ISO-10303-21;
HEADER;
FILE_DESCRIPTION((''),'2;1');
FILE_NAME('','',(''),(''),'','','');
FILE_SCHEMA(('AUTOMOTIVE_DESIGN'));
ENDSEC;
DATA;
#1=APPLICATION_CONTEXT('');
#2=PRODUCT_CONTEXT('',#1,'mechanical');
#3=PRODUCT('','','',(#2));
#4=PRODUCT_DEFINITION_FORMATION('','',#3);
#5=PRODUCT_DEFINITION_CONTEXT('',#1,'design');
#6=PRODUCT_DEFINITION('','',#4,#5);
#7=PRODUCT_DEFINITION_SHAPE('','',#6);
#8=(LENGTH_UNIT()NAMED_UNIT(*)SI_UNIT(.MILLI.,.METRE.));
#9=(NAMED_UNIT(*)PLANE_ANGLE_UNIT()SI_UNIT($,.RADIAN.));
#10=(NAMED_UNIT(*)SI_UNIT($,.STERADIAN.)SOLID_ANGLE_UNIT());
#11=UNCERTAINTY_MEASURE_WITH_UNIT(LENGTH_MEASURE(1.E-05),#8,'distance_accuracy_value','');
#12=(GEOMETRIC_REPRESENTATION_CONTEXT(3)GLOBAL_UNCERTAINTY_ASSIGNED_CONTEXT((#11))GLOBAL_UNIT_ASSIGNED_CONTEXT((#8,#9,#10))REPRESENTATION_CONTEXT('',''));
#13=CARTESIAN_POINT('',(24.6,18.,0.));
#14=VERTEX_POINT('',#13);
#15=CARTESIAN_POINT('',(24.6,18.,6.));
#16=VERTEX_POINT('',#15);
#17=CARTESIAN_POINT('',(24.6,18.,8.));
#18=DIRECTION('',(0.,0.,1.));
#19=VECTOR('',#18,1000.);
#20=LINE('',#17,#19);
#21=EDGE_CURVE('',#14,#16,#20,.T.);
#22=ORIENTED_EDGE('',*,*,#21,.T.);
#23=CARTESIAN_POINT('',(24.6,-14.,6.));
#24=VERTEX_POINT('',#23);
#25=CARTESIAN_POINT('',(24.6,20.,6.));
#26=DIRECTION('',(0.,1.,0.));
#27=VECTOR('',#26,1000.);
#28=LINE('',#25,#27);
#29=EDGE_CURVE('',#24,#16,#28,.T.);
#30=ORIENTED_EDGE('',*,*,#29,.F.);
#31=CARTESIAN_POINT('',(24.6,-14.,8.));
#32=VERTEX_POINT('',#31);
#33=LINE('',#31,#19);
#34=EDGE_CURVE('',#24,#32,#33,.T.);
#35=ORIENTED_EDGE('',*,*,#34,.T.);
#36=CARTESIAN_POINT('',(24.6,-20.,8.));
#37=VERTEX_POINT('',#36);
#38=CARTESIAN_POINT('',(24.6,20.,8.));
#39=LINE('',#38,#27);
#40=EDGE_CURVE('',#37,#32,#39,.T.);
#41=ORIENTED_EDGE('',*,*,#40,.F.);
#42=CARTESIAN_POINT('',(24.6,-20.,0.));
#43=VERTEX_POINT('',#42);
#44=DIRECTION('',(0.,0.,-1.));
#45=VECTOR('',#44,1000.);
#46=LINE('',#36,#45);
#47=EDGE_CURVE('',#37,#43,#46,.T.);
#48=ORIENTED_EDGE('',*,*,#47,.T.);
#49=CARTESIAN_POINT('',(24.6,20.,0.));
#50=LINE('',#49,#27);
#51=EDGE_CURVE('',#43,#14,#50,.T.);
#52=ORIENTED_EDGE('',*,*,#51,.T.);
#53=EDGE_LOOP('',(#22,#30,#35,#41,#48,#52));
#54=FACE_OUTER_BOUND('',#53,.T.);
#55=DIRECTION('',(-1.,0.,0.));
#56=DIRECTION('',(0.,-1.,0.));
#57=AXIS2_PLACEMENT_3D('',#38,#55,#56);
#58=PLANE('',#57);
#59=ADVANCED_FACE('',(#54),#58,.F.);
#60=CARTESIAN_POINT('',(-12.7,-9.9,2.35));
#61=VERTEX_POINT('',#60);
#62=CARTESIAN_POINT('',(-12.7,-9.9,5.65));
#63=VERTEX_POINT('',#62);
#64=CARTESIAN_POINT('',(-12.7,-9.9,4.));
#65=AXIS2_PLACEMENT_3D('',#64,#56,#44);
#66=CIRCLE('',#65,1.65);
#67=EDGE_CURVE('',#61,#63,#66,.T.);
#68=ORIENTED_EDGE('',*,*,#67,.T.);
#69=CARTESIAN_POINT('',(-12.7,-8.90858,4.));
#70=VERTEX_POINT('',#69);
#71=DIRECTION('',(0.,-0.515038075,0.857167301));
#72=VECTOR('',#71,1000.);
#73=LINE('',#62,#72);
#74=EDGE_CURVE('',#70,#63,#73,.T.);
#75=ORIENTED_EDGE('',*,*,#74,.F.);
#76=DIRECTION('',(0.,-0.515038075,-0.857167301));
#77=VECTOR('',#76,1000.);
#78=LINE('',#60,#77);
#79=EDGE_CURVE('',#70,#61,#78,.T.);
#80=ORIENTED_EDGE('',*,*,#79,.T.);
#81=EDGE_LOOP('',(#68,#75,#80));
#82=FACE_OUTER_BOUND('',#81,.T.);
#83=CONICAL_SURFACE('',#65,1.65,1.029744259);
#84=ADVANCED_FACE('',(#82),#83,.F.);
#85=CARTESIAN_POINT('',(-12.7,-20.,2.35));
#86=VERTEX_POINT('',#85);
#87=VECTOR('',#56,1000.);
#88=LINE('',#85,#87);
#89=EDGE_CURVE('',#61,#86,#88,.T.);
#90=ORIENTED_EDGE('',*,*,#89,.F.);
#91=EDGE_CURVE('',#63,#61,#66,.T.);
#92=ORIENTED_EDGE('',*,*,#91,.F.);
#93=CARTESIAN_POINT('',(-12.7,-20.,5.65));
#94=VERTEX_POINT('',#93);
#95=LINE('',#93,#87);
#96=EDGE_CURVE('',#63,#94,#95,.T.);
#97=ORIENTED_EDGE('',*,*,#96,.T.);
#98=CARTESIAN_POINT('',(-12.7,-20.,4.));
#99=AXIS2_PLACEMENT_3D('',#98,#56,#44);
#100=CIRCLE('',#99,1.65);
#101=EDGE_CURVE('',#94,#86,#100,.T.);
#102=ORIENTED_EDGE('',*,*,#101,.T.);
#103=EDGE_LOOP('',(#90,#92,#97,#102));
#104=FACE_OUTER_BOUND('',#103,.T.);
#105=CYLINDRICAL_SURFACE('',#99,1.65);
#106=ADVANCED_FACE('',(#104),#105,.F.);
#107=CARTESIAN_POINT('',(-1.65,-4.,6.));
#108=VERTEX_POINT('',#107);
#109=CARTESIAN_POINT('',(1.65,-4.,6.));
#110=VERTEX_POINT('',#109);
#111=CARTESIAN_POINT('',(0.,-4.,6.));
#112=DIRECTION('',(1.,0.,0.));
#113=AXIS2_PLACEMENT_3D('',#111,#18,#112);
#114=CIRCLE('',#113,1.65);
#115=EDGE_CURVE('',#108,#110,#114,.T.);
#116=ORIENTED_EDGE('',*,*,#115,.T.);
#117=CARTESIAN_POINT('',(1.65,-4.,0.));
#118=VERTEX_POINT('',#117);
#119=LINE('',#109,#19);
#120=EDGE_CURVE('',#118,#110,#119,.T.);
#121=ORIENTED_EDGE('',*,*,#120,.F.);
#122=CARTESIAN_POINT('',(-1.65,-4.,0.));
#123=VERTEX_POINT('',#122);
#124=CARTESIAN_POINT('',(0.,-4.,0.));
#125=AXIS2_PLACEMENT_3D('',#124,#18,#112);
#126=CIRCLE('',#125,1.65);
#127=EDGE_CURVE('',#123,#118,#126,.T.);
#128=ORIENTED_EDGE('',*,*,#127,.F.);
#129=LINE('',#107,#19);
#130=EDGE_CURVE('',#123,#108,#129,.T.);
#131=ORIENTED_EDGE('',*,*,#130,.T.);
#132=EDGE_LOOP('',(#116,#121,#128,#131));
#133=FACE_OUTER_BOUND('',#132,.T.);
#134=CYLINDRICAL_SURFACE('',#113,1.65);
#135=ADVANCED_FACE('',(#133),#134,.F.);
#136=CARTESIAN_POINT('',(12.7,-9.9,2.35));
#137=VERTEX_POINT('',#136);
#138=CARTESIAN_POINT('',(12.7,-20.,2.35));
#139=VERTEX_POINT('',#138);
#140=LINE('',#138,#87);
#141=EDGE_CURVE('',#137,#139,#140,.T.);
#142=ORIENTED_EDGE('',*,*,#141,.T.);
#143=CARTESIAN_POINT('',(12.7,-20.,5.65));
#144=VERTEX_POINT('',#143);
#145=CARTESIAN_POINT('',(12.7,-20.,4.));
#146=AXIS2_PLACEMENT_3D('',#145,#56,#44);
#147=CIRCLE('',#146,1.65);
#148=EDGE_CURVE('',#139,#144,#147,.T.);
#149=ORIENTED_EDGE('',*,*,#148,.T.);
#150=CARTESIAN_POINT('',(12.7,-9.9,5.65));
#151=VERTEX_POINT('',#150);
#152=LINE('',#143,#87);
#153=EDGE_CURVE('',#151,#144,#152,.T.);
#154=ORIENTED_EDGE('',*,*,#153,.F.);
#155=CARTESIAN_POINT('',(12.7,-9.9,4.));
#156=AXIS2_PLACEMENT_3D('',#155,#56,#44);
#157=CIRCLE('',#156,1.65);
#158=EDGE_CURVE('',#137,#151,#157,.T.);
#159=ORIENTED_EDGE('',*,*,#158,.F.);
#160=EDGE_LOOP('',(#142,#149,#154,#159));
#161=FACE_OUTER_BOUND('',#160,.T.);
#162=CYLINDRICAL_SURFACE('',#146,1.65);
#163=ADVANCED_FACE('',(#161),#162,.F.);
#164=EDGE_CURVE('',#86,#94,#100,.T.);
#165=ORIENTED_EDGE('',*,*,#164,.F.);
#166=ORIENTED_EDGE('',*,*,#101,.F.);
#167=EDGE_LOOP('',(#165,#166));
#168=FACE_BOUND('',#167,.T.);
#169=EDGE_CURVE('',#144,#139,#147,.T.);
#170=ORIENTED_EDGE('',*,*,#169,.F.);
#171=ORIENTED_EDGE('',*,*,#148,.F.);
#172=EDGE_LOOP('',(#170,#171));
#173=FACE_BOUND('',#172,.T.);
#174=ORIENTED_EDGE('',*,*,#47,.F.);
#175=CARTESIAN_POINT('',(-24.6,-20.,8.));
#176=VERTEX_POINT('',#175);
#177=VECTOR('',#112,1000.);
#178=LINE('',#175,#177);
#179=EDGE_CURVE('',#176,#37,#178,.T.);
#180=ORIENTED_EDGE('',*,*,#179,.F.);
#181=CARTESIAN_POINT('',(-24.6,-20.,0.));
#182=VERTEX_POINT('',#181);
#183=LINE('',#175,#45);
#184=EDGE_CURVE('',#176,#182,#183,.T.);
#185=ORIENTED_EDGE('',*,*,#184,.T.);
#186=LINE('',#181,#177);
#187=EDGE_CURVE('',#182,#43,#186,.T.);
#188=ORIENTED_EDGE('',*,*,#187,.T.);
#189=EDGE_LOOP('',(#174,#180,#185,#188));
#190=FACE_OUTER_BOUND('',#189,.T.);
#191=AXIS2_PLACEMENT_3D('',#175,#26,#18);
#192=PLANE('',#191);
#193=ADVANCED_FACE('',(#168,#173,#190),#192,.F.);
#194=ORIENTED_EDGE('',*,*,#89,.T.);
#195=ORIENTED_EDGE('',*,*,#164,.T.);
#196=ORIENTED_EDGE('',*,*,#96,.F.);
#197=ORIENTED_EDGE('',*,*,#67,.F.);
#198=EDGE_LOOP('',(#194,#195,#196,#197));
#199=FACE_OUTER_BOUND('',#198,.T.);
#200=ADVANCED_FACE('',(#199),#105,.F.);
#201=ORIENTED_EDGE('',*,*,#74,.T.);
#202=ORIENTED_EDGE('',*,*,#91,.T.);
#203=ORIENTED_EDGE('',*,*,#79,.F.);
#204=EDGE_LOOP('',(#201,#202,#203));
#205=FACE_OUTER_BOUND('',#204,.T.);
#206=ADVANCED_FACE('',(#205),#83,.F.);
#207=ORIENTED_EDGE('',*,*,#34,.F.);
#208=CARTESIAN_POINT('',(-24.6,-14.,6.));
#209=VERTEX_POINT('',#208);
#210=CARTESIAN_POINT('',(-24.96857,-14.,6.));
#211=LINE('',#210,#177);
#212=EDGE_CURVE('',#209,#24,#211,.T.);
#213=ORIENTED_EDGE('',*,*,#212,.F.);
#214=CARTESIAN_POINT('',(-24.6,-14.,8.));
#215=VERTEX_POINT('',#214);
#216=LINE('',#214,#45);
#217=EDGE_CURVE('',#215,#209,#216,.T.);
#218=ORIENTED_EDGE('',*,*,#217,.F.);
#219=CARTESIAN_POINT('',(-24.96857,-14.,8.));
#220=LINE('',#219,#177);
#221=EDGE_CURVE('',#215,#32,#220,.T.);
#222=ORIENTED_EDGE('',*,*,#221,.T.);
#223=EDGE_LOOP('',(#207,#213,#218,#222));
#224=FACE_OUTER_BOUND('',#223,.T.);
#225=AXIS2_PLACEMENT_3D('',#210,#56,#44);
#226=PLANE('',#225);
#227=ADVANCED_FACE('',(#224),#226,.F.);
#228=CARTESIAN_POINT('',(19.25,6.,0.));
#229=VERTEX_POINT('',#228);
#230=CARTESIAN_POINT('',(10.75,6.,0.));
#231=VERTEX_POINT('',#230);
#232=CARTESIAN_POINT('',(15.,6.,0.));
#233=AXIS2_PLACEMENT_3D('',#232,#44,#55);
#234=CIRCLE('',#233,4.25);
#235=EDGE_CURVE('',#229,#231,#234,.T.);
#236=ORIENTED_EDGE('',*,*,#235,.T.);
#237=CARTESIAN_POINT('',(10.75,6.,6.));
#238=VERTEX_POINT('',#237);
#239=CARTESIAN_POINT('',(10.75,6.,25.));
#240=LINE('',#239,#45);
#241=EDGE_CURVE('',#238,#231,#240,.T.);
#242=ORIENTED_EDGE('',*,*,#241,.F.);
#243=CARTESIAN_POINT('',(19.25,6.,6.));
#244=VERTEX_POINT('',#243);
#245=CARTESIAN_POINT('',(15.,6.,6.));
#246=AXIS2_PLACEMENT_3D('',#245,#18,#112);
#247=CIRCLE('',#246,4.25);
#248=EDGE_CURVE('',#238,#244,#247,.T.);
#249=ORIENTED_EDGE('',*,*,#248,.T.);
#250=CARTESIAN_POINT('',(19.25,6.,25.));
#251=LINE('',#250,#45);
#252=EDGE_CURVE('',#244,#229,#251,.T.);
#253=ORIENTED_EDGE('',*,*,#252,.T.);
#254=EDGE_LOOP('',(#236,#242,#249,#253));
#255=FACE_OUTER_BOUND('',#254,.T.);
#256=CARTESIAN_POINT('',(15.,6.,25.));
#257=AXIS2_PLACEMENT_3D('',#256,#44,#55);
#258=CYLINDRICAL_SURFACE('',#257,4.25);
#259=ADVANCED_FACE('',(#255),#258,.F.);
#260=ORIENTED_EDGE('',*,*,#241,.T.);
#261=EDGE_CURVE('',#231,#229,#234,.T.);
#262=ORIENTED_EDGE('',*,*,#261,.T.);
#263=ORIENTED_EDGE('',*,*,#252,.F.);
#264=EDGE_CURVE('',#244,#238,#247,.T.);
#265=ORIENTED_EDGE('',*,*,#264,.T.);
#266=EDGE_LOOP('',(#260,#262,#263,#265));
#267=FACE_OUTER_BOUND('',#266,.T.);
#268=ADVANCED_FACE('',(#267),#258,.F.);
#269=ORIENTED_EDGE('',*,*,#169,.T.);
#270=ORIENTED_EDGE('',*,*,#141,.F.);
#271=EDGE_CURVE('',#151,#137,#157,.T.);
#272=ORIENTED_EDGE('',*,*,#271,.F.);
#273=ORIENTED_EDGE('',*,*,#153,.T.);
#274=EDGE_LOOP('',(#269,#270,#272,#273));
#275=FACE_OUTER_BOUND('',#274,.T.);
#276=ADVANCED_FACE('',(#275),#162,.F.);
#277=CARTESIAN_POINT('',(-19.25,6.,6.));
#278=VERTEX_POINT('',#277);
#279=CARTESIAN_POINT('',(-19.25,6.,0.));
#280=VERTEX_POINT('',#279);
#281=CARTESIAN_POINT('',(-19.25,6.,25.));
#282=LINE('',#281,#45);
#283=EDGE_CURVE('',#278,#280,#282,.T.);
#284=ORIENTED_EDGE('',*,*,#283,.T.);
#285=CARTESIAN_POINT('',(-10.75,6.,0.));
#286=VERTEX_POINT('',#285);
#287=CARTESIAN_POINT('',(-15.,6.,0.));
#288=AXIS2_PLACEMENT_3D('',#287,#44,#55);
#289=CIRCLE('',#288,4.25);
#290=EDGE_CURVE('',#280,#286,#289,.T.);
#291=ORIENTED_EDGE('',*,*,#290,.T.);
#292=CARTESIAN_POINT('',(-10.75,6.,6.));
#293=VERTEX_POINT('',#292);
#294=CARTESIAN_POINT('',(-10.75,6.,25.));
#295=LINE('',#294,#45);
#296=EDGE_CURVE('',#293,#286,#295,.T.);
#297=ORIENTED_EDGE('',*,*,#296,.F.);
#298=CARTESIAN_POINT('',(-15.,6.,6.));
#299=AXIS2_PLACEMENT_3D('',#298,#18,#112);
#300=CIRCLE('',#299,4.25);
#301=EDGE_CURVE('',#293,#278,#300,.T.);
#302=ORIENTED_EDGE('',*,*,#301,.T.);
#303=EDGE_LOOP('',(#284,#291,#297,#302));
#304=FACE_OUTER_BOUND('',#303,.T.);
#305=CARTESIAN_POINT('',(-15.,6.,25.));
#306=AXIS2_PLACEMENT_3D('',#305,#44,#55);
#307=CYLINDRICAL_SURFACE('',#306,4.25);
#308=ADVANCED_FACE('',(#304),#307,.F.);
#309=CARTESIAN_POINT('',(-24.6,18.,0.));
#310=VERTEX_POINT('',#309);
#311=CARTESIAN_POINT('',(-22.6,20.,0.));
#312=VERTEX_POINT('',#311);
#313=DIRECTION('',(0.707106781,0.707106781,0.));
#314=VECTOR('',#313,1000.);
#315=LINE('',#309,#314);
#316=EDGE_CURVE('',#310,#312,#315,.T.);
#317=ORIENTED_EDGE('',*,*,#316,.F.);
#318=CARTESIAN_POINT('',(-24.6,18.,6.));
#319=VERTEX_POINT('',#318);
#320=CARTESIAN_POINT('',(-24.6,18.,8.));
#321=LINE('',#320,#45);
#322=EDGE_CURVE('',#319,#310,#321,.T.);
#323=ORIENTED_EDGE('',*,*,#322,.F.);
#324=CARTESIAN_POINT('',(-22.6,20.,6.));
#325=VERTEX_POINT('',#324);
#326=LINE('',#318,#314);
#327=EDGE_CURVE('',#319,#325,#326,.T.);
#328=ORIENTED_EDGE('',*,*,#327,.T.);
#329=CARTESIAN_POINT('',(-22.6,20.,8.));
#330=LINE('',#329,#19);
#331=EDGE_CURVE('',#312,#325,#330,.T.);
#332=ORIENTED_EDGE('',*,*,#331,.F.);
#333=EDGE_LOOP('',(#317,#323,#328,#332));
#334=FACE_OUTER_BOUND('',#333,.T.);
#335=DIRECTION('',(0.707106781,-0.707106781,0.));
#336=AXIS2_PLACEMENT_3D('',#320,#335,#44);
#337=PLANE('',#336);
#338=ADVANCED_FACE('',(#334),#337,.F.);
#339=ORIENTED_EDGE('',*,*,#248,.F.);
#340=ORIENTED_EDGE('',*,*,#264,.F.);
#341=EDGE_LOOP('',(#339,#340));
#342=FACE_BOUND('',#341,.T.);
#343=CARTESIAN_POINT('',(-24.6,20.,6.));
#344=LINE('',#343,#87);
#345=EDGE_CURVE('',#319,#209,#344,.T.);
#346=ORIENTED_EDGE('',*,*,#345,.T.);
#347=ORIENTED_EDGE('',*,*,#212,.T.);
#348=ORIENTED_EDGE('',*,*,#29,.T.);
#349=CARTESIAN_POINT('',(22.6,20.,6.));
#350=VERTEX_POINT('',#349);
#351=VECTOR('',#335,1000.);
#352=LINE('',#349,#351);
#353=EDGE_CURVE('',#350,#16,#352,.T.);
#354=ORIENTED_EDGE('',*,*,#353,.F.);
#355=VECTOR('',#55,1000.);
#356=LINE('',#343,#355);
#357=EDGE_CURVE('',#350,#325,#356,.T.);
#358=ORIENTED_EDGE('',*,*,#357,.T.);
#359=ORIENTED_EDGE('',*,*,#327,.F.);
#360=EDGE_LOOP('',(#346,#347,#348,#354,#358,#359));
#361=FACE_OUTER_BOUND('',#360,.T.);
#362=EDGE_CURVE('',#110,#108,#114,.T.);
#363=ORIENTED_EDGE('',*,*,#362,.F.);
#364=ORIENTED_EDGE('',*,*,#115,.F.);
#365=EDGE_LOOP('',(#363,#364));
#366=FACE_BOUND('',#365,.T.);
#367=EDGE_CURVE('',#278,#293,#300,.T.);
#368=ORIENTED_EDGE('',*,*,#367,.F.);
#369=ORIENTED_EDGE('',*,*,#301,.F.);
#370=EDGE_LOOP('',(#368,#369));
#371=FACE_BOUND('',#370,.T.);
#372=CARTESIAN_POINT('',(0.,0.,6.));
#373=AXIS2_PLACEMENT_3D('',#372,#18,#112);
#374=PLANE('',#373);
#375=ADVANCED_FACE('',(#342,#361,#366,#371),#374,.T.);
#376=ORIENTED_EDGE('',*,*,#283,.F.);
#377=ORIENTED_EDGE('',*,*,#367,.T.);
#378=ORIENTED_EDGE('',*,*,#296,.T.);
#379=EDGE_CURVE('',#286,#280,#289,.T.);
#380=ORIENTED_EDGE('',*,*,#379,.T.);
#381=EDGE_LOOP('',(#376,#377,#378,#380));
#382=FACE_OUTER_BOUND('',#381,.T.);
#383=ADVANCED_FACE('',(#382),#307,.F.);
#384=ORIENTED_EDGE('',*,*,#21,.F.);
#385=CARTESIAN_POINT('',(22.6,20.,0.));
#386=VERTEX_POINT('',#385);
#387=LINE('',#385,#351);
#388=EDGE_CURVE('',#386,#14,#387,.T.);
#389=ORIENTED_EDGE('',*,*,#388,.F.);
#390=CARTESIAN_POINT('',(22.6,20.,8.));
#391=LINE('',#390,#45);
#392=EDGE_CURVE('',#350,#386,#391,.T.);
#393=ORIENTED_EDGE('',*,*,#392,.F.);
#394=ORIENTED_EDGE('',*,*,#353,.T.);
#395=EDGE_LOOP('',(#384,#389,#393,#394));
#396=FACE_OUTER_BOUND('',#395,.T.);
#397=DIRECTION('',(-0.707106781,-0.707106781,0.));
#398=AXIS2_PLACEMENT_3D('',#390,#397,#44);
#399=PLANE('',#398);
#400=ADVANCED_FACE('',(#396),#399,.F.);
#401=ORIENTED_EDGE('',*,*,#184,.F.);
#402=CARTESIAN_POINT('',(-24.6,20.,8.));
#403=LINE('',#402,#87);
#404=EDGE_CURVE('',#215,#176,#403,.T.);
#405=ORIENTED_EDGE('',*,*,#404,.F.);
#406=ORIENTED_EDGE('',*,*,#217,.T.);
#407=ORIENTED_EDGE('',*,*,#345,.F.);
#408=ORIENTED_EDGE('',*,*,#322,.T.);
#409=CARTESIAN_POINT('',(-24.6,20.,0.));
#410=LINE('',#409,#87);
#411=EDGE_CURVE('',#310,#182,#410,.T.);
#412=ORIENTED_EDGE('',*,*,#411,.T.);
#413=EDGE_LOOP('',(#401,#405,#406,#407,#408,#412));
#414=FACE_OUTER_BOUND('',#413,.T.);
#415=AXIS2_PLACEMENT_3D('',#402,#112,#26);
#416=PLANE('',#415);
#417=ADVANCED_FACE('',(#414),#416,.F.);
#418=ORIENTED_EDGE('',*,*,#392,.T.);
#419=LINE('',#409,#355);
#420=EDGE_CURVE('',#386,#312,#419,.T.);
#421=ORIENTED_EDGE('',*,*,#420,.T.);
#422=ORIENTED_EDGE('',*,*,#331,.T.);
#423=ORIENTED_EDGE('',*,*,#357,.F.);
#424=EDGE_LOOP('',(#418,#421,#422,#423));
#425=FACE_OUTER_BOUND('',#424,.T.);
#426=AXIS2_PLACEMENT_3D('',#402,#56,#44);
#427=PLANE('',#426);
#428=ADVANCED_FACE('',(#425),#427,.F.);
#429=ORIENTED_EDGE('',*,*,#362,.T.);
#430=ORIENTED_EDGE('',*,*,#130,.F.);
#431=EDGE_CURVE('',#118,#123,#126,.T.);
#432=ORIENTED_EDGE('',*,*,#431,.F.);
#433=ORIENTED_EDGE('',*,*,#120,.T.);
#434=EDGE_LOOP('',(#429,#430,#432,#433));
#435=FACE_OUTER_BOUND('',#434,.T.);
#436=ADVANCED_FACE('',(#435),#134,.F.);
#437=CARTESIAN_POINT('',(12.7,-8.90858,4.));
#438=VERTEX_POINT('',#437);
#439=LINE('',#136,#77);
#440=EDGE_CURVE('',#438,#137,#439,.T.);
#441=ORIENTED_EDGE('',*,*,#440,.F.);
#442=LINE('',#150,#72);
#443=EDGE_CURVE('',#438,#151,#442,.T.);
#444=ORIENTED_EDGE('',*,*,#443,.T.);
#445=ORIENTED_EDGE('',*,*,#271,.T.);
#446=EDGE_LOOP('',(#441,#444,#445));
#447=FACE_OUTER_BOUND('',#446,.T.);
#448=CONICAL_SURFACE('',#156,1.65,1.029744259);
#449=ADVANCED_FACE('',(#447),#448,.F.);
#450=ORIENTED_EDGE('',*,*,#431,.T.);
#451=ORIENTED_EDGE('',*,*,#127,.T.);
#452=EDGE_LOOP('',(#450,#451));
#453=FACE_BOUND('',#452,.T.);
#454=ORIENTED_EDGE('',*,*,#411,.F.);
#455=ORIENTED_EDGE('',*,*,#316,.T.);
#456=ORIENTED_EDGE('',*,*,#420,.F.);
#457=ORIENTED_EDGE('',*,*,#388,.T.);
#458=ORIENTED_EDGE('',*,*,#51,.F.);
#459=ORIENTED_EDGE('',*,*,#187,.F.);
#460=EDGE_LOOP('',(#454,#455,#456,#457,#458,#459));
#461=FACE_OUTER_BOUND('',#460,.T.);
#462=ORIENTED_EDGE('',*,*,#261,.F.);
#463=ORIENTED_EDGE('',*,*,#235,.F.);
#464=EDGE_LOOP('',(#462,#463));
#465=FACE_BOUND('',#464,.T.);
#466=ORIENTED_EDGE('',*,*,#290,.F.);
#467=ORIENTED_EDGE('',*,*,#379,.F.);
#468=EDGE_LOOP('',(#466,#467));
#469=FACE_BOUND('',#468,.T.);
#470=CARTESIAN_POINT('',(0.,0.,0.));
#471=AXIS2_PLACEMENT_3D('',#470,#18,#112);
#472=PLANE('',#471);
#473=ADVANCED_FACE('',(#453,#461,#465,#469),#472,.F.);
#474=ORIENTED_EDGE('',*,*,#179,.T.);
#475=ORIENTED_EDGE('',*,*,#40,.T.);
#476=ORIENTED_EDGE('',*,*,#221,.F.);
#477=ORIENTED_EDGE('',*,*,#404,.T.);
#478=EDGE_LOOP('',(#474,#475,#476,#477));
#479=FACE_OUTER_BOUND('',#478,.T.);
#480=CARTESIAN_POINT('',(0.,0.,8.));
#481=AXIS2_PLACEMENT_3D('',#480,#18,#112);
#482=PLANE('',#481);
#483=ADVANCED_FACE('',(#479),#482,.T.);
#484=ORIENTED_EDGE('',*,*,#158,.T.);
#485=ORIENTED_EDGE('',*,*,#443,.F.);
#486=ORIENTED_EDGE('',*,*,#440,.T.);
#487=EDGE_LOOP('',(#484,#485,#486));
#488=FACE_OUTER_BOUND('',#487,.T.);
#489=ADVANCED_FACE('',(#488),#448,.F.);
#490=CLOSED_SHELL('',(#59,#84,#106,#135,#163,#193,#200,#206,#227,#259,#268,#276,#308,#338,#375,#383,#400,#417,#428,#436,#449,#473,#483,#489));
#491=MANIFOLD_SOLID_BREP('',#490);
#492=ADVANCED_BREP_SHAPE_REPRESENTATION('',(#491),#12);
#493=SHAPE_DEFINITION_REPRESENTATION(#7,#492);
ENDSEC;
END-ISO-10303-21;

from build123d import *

# Parameters (mm, degrees)
SKETCH_1_W             = 49.2
SKETCH_1_H             = 40
EXTRUDE_1_DEPTH        = 8
HOLE_WIZARD_M4_1_D     = 3.3
HOLE_WIZARD_M4_1_DEPTH = 10.1
HOLE_WIZARD_M4_1_TIP   = 0.991420021
CHAMFER_1_SIZE         = 2
SKETCH_8_W             = 55.272888483
SKETCH_8_H             = 36.198084545
CUT_EXTRUDE_3_DEPTH    = 2
SKETCH_9_R             = 4.25
CUT_EXTRUDE_4_DEPTH    = 25
HOLE_WIZARD_M4_2_D     = 3.3
HOLE_WIZARD_M4_2_DEPTH = 10.1
HOLE_WIZARD_M4_2_TIP   = 0.991420021


with BuildPart() as part:
    # 草图1 → 凸台-拉伸1 (new body)
    with BuildSketch(Plane.XY):
        Rectangle(SKETCH_1_W, SKETCH_1_H)
    extrude(amount=EXTRUDE_1_DEPTH)

    # M4 螺纹孔1
    with Locations(Plane(origin=(0, -20, 0), x_dir=(-1, 0, 0), z_dir=(0, -1, 0))):
        with Locations((12.7, -4), (-12.7, -4)):
            Hole(HOLE_WIZARD_M4_1_D / 2, depth=HOLE_WIZARD_M4_1_DEPTH)
            with Locations((0, 0, -(HOLE_WIZARD_M4_1_DEPTH + HOLE_WIZARD_M4_1_TIP / 2))):  # 118° drill point
                Cone(0, HOLE_WIZARD_M4_1_D / 2, HOLE_WIZARD_M4_1_TIP, mode=Mode.SUBTRACT)

    # 倒角1
    chamfer_1_edges = [part.edges().sort_by_distance(p)[0] for p in [
        (-24.6, 20, 4),
        (24.6, 20, 4),
    ]]
    chamfer(chamfer_1_edges, length=CHAMFER_1_SIZE)

    # 草图8 → 切除-拉伸3 (cut)
    with BuildSketch(Plane.XY.offset(8)):
        with Locations((2.667874568, 4.099042273)):
            Rectangle(SKETCH_8_W, SKETCH_8_H)
    extrude(amount=-CUT_EXTRUDE_3_DEPTH, mode=Mode.SUBTRACT)

    # 草图9 → 切除-拉伸4 (cut)
    with BuildSketch(Plane(origin=(0, 0, 0), x_dir=(-1, 0, 0), z_dir=(0, 0, -1))):
        with Locations((-15, 6)):
            Circle(SKETCH_9_R)
        with Locations((15, 6)):
            Circle(SKETCH_9_R)
    extrude(amount=-CUT_EXTRUDE_4_DEPTH, mode=Mode.SUBTRACT)

    # M4 螺纹孔2
    with Locations(Plane.XY.offset(6)):
        with Locations((0, -4)):
            Hole(HOLE_WIZARD_M4_2_D / 2, depth=HOLE_WIZARD_M4_2_DEPTH)
            with Locations((0, 0, -(HOLE_WIZARD_M4_2_DEPTH + HOLE_WIZARD_M4_2_TIP / 2))):  # 118° drill point
                Cone(0, HOLE_WIZARD_M4_2_D / 2, HOLE_WIZARD_M4_2_TIP, mode=Mode.SUBTRACT)


solid = part.part
